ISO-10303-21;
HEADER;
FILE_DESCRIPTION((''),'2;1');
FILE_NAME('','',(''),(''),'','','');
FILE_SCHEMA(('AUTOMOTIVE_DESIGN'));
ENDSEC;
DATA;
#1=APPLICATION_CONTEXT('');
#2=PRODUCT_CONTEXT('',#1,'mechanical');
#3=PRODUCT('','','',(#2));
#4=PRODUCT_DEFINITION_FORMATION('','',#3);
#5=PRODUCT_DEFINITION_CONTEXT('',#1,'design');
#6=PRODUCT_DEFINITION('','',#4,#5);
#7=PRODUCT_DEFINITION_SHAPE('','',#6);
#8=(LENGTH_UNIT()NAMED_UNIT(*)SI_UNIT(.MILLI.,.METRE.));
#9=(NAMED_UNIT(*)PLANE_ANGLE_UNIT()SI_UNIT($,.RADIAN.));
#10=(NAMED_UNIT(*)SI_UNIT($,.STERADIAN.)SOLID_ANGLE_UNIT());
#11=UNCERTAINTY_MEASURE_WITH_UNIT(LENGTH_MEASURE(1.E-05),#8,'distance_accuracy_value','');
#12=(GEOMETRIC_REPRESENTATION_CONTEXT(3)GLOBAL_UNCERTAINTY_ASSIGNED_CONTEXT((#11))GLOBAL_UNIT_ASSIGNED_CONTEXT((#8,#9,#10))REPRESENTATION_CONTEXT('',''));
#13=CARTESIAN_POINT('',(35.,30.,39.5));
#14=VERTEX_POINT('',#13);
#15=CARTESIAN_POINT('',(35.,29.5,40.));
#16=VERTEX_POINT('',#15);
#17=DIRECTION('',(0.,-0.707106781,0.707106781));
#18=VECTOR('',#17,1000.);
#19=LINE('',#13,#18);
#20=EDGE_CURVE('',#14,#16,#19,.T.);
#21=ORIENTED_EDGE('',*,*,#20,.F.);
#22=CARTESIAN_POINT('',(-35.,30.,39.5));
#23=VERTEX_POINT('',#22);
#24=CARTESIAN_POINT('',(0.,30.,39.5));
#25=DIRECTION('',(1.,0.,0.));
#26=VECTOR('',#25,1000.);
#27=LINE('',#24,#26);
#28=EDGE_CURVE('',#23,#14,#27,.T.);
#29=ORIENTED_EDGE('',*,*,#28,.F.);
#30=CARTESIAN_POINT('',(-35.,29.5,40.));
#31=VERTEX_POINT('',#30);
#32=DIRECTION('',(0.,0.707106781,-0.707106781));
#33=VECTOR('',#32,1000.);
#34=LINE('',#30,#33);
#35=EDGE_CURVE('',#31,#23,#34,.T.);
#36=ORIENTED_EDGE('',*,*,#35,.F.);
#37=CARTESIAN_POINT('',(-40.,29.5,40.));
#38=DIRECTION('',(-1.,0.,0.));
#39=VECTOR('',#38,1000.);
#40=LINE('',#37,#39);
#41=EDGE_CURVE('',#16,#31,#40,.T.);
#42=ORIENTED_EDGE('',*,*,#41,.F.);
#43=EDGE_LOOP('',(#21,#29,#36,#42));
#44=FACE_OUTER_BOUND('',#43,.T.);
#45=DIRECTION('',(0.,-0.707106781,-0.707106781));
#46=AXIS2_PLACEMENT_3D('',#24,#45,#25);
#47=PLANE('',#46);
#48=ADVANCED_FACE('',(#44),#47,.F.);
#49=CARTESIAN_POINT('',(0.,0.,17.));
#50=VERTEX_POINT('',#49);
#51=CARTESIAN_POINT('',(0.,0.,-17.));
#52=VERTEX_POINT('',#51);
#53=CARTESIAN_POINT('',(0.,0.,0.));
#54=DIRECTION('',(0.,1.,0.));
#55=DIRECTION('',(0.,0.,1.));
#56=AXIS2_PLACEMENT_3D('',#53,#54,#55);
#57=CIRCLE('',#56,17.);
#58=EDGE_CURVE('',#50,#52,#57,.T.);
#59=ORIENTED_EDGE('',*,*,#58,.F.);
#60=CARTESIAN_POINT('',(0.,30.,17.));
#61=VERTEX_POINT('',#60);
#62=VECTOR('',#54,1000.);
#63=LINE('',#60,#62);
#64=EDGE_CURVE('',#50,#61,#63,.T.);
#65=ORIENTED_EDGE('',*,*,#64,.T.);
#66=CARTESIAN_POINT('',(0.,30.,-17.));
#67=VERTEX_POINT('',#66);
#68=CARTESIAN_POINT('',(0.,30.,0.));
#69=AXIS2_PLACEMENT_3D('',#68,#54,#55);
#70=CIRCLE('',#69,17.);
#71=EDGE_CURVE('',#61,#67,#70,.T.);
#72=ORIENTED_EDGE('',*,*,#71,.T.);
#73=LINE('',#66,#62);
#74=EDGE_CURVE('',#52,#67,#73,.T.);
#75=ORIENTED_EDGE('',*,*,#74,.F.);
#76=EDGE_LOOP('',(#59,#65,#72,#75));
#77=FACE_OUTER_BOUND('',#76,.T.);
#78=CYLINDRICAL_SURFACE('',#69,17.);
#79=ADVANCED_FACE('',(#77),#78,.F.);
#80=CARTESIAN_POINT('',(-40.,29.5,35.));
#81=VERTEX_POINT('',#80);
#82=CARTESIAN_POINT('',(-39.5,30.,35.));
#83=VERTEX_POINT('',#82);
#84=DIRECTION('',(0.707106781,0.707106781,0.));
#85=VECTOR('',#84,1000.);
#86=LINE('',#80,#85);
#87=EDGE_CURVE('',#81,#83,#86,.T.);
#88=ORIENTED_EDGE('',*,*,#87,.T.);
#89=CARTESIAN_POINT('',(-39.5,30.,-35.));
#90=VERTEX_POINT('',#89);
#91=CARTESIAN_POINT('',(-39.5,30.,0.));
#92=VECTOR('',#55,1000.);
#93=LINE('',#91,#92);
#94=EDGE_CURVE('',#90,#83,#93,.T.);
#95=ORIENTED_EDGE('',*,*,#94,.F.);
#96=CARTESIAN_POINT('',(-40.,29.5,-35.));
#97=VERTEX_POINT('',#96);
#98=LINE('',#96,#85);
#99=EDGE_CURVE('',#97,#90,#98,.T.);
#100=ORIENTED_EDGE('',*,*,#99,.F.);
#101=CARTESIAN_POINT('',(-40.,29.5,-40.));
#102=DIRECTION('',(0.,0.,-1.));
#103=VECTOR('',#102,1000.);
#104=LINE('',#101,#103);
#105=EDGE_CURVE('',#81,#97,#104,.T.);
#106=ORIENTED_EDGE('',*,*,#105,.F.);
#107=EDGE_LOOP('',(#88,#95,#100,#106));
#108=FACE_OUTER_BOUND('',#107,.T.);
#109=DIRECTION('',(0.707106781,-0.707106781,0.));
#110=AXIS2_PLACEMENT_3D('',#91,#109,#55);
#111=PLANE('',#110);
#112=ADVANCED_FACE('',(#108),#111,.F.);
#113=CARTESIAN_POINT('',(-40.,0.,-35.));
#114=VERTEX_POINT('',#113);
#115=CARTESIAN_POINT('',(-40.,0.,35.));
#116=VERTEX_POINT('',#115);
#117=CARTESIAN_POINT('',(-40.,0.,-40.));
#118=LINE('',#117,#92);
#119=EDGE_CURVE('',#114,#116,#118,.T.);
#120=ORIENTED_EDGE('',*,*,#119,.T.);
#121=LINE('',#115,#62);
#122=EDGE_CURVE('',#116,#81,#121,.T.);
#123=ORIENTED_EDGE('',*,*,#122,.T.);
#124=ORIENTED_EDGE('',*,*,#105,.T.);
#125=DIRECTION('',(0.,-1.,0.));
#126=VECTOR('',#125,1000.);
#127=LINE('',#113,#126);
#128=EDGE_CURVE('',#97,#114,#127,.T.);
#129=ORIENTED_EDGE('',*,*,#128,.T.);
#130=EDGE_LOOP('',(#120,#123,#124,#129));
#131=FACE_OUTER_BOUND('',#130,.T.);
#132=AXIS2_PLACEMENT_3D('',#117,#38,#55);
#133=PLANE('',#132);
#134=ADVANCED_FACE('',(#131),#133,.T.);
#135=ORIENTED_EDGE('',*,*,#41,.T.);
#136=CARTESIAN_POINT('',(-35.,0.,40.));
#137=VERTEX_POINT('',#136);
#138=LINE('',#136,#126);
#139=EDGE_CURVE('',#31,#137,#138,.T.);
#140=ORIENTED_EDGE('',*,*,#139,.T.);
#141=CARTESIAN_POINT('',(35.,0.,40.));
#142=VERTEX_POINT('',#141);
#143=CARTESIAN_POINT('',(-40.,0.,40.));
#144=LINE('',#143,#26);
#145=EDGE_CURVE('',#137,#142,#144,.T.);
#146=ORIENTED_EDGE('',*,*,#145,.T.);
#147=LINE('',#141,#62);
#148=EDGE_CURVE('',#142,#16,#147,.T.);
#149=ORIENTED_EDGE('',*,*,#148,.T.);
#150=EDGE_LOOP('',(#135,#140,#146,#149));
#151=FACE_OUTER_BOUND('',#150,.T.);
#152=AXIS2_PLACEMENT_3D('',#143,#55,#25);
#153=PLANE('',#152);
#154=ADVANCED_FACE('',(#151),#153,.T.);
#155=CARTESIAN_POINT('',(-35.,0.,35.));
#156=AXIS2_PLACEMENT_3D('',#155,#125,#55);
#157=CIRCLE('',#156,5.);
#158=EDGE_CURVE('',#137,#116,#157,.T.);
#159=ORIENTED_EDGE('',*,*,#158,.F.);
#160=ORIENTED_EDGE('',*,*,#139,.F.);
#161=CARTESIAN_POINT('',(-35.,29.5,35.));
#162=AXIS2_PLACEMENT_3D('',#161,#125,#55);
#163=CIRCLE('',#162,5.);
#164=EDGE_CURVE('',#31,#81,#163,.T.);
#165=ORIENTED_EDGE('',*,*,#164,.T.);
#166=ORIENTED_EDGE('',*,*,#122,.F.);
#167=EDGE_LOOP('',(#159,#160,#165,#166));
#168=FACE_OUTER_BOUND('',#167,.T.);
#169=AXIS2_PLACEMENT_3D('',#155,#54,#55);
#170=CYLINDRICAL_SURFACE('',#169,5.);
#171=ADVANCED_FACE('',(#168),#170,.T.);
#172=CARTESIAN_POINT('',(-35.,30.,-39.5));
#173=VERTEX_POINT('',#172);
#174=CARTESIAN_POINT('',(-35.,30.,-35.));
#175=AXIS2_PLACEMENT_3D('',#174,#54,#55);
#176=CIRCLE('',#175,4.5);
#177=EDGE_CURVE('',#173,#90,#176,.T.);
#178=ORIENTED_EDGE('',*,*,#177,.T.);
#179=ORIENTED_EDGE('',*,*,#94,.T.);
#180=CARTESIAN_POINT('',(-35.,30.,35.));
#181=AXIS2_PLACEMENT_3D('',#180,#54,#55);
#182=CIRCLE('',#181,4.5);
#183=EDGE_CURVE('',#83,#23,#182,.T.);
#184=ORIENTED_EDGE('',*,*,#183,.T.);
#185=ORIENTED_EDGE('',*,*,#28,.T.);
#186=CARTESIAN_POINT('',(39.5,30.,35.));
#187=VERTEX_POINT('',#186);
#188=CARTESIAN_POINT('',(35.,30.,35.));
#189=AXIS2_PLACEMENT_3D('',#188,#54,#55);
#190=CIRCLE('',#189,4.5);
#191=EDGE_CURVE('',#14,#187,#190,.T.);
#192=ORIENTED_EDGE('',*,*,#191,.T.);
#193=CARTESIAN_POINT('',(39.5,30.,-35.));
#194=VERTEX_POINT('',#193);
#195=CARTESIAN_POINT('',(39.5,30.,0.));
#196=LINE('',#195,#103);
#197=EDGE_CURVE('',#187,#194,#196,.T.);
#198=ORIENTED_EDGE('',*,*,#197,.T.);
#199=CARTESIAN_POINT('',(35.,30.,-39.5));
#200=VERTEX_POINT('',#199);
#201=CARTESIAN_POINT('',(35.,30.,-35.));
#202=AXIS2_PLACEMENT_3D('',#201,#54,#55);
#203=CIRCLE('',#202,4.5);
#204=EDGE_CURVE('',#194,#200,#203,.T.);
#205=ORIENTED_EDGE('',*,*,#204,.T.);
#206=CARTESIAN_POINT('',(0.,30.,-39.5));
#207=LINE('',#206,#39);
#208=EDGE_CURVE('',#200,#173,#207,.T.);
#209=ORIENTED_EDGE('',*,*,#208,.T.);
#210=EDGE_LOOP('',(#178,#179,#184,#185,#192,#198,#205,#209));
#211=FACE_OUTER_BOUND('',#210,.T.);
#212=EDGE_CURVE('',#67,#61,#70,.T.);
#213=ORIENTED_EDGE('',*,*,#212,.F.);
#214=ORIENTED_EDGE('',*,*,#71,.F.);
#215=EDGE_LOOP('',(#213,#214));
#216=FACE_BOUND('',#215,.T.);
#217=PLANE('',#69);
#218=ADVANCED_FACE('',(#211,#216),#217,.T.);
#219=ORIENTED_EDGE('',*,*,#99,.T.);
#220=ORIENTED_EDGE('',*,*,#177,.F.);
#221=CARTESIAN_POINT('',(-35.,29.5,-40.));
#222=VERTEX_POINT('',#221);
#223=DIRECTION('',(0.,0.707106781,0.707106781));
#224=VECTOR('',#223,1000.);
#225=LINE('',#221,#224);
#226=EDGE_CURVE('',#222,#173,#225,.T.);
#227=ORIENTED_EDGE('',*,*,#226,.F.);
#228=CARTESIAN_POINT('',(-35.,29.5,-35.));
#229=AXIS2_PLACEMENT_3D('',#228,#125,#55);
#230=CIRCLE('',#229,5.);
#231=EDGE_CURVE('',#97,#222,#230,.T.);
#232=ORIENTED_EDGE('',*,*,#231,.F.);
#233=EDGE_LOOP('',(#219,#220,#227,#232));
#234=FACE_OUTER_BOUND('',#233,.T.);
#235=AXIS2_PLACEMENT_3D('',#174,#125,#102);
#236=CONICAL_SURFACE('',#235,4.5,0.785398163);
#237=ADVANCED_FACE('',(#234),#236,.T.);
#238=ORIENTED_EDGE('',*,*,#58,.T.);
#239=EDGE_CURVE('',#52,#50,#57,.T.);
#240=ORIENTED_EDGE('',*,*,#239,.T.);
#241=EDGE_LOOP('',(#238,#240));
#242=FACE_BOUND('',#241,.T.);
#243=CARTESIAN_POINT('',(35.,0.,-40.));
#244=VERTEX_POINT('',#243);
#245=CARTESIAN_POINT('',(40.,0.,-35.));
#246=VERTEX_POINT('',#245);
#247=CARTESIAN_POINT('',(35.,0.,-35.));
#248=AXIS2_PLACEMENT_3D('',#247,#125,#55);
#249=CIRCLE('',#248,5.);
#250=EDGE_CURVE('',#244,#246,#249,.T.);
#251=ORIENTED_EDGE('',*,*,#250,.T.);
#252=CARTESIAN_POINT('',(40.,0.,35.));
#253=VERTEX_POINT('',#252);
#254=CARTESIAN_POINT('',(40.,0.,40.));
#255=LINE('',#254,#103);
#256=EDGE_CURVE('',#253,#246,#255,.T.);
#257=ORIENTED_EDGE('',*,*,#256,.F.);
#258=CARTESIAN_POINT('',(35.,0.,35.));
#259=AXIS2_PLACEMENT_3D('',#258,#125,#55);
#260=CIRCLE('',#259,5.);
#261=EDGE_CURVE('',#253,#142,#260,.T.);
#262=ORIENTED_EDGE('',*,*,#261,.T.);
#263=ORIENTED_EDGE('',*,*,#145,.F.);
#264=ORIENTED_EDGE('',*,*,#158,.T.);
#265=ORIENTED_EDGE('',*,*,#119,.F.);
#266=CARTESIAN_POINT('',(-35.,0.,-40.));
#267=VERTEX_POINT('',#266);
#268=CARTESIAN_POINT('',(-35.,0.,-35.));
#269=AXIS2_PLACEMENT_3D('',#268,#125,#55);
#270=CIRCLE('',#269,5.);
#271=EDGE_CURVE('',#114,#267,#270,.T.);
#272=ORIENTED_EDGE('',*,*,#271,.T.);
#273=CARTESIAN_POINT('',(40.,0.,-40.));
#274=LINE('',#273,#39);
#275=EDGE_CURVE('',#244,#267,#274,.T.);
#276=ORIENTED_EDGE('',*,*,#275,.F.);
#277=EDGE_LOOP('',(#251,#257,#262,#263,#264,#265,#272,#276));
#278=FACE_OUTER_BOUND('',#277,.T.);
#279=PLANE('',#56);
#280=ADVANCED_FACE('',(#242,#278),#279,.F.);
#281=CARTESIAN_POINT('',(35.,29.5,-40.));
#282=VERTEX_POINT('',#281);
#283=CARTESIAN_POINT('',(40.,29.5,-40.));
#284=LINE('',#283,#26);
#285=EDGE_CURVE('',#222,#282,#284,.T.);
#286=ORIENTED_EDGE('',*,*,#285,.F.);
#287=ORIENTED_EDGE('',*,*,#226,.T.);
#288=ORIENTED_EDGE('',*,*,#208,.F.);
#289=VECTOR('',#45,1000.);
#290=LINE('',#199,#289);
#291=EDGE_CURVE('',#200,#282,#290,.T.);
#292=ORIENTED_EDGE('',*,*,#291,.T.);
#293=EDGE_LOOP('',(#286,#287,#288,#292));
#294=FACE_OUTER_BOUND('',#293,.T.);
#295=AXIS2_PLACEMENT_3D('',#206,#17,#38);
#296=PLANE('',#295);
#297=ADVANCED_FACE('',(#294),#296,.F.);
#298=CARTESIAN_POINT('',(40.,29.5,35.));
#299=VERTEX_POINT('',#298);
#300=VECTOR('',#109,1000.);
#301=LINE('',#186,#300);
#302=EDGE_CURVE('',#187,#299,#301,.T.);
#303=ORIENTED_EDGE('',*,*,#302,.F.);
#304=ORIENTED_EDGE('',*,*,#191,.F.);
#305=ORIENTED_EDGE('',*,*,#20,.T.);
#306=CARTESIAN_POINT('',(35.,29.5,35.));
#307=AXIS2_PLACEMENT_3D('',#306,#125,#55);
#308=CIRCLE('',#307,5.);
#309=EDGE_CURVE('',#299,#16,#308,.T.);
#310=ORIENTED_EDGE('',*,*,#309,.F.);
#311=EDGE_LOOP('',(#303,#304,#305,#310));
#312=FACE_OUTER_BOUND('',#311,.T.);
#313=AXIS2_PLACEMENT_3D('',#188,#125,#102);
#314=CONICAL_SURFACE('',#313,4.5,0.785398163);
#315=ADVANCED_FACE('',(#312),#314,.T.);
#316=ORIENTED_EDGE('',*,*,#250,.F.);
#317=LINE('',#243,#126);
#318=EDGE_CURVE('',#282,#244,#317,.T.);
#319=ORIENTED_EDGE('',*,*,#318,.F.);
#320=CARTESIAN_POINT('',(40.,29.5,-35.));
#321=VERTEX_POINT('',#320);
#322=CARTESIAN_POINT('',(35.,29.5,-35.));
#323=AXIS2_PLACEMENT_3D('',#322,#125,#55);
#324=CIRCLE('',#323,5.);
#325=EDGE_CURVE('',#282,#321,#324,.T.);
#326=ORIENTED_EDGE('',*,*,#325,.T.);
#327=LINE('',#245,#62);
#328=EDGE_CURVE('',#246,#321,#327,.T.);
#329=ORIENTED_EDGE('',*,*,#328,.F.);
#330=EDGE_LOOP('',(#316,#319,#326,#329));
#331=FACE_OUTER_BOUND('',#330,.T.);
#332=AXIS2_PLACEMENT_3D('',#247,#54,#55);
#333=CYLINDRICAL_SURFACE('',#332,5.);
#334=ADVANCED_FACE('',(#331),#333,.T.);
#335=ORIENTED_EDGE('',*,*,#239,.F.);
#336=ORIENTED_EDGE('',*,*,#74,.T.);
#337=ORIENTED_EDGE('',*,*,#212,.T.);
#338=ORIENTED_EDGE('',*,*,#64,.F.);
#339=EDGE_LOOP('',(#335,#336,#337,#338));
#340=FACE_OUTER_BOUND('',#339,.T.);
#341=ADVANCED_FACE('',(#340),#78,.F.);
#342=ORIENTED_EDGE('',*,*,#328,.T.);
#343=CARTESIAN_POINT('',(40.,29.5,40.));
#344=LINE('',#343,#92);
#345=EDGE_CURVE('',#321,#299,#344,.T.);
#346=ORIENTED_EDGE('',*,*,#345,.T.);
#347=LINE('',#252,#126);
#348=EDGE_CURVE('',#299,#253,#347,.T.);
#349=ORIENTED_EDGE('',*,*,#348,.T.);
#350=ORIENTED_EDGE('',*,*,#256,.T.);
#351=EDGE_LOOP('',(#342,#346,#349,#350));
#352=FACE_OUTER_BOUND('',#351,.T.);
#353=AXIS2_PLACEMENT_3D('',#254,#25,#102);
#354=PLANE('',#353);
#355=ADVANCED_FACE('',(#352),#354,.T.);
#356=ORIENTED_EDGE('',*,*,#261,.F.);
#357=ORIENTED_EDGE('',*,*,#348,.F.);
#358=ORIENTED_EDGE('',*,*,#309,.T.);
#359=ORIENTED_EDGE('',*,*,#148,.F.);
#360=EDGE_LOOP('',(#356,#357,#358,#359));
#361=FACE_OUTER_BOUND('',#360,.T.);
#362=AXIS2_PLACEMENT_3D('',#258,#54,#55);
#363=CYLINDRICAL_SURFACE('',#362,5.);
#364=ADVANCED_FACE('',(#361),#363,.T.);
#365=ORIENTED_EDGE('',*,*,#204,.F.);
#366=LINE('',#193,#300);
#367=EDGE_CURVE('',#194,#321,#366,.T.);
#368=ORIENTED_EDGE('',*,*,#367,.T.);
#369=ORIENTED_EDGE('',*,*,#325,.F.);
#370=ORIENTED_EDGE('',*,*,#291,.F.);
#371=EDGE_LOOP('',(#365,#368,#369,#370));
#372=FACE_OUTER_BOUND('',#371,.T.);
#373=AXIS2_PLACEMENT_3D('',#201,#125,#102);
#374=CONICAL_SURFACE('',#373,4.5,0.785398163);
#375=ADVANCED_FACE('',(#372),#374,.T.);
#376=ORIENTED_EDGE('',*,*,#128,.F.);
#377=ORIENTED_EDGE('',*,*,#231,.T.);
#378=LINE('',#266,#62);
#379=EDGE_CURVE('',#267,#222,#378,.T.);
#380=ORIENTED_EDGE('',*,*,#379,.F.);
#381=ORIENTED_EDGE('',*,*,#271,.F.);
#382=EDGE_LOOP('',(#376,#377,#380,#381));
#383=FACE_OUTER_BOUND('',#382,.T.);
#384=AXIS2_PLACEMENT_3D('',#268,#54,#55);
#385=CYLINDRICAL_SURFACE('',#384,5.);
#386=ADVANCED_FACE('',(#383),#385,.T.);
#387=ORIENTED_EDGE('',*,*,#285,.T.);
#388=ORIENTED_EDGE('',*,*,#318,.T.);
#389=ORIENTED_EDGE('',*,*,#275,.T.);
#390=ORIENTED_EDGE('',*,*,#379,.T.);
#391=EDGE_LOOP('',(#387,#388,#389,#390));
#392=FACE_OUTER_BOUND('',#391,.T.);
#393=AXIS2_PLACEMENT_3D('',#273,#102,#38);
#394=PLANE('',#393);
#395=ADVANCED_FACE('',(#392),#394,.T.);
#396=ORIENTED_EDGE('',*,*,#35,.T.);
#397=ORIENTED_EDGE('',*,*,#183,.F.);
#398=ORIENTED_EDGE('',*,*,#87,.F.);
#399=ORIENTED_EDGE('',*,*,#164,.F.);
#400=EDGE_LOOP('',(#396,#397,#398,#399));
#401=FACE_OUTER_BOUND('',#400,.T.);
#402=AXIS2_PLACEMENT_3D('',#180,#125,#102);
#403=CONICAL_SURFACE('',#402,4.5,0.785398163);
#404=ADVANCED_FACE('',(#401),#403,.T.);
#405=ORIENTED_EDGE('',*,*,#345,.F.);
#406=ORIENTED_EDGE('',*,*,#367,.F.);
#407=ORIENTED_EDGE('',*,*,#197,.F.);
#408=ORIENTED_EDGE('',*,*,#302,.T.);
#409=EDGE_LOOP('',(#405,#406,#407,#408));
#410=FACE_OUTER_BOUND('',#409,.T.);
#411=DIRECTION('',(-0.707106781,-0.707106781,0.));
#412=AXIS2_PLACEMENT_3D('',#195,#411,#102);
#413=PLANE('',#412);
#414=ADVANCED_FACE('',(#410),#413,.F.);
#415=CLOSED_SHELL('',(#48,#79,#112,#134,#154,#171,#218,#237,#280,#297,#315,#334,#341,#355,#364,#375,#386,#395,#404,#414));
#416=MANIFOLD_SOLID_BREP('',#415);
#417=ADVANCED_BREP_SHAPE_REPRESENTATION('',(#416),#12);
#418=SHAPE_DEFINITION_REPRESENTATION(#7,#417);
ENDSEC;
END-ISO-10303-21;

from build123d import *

# Parameters (mm, degrees)
SKETCH1_W              = 80
SKETCH1_H              = 80
BOSS_EXTRUDE1_DEPTH    = 30
M36X2_0_TAPPED_HOLE1_D = 34
FILLET1_R              = 5
CHAMFER1_SIZE          = 0.5


with BuildPart() as part:
    # Sketch1 → Boss-Extrude1 (new body)
    with BuildSketch(Plane(origin=(0, 30, 0), x_dir=(1, 0, 0), z_dir=(0, 1, 0))):
        Rectangle(SKETCH1_W, SKETCH1_H)
    extrude(amount=-BOSS_EXTRUDE1_DEPTH)

    # M36x2.0 Tapped Hole1 (through all)
    with Locations(Plane(origin=(0, 30, 0), x_dir=(1, 0, 0), z_dir=(0, 1, 0))):
        with Locations((0, 0)):
            Hole(M36X2_0_TAPPED_HOLE1_D / 2)

    # Fillet1
    fillet1_edges = [part.edges().sort_by_distance(p)[0] for p in [
        (-40, 15, -40),
        (40, 15, -40),
        (40, 15, 40),
        (-40, 15, 40),
    ]]
    fillet(fillet1_edges, radius=FILLET1_R)

    # Chamfer1
    chamfer1_edges = [part.edges().sort_by_distance(p)[0] for p in [
        (0, 30, 40),
        (-40, 30, 0),
        (40, 30, 0),
        (0, 30, -40),
        (-38.535533906, 30, -38.535533906),
        (38.535533906, 30, -38.535533906),
        (-38.535533906, 30, 38.535533906),
        (38.535533906, 30, 38.535533906),
    ]]
    chamfer(chamfer1_edges, length=CHAMFER1_SIZE)


solid = part.part
